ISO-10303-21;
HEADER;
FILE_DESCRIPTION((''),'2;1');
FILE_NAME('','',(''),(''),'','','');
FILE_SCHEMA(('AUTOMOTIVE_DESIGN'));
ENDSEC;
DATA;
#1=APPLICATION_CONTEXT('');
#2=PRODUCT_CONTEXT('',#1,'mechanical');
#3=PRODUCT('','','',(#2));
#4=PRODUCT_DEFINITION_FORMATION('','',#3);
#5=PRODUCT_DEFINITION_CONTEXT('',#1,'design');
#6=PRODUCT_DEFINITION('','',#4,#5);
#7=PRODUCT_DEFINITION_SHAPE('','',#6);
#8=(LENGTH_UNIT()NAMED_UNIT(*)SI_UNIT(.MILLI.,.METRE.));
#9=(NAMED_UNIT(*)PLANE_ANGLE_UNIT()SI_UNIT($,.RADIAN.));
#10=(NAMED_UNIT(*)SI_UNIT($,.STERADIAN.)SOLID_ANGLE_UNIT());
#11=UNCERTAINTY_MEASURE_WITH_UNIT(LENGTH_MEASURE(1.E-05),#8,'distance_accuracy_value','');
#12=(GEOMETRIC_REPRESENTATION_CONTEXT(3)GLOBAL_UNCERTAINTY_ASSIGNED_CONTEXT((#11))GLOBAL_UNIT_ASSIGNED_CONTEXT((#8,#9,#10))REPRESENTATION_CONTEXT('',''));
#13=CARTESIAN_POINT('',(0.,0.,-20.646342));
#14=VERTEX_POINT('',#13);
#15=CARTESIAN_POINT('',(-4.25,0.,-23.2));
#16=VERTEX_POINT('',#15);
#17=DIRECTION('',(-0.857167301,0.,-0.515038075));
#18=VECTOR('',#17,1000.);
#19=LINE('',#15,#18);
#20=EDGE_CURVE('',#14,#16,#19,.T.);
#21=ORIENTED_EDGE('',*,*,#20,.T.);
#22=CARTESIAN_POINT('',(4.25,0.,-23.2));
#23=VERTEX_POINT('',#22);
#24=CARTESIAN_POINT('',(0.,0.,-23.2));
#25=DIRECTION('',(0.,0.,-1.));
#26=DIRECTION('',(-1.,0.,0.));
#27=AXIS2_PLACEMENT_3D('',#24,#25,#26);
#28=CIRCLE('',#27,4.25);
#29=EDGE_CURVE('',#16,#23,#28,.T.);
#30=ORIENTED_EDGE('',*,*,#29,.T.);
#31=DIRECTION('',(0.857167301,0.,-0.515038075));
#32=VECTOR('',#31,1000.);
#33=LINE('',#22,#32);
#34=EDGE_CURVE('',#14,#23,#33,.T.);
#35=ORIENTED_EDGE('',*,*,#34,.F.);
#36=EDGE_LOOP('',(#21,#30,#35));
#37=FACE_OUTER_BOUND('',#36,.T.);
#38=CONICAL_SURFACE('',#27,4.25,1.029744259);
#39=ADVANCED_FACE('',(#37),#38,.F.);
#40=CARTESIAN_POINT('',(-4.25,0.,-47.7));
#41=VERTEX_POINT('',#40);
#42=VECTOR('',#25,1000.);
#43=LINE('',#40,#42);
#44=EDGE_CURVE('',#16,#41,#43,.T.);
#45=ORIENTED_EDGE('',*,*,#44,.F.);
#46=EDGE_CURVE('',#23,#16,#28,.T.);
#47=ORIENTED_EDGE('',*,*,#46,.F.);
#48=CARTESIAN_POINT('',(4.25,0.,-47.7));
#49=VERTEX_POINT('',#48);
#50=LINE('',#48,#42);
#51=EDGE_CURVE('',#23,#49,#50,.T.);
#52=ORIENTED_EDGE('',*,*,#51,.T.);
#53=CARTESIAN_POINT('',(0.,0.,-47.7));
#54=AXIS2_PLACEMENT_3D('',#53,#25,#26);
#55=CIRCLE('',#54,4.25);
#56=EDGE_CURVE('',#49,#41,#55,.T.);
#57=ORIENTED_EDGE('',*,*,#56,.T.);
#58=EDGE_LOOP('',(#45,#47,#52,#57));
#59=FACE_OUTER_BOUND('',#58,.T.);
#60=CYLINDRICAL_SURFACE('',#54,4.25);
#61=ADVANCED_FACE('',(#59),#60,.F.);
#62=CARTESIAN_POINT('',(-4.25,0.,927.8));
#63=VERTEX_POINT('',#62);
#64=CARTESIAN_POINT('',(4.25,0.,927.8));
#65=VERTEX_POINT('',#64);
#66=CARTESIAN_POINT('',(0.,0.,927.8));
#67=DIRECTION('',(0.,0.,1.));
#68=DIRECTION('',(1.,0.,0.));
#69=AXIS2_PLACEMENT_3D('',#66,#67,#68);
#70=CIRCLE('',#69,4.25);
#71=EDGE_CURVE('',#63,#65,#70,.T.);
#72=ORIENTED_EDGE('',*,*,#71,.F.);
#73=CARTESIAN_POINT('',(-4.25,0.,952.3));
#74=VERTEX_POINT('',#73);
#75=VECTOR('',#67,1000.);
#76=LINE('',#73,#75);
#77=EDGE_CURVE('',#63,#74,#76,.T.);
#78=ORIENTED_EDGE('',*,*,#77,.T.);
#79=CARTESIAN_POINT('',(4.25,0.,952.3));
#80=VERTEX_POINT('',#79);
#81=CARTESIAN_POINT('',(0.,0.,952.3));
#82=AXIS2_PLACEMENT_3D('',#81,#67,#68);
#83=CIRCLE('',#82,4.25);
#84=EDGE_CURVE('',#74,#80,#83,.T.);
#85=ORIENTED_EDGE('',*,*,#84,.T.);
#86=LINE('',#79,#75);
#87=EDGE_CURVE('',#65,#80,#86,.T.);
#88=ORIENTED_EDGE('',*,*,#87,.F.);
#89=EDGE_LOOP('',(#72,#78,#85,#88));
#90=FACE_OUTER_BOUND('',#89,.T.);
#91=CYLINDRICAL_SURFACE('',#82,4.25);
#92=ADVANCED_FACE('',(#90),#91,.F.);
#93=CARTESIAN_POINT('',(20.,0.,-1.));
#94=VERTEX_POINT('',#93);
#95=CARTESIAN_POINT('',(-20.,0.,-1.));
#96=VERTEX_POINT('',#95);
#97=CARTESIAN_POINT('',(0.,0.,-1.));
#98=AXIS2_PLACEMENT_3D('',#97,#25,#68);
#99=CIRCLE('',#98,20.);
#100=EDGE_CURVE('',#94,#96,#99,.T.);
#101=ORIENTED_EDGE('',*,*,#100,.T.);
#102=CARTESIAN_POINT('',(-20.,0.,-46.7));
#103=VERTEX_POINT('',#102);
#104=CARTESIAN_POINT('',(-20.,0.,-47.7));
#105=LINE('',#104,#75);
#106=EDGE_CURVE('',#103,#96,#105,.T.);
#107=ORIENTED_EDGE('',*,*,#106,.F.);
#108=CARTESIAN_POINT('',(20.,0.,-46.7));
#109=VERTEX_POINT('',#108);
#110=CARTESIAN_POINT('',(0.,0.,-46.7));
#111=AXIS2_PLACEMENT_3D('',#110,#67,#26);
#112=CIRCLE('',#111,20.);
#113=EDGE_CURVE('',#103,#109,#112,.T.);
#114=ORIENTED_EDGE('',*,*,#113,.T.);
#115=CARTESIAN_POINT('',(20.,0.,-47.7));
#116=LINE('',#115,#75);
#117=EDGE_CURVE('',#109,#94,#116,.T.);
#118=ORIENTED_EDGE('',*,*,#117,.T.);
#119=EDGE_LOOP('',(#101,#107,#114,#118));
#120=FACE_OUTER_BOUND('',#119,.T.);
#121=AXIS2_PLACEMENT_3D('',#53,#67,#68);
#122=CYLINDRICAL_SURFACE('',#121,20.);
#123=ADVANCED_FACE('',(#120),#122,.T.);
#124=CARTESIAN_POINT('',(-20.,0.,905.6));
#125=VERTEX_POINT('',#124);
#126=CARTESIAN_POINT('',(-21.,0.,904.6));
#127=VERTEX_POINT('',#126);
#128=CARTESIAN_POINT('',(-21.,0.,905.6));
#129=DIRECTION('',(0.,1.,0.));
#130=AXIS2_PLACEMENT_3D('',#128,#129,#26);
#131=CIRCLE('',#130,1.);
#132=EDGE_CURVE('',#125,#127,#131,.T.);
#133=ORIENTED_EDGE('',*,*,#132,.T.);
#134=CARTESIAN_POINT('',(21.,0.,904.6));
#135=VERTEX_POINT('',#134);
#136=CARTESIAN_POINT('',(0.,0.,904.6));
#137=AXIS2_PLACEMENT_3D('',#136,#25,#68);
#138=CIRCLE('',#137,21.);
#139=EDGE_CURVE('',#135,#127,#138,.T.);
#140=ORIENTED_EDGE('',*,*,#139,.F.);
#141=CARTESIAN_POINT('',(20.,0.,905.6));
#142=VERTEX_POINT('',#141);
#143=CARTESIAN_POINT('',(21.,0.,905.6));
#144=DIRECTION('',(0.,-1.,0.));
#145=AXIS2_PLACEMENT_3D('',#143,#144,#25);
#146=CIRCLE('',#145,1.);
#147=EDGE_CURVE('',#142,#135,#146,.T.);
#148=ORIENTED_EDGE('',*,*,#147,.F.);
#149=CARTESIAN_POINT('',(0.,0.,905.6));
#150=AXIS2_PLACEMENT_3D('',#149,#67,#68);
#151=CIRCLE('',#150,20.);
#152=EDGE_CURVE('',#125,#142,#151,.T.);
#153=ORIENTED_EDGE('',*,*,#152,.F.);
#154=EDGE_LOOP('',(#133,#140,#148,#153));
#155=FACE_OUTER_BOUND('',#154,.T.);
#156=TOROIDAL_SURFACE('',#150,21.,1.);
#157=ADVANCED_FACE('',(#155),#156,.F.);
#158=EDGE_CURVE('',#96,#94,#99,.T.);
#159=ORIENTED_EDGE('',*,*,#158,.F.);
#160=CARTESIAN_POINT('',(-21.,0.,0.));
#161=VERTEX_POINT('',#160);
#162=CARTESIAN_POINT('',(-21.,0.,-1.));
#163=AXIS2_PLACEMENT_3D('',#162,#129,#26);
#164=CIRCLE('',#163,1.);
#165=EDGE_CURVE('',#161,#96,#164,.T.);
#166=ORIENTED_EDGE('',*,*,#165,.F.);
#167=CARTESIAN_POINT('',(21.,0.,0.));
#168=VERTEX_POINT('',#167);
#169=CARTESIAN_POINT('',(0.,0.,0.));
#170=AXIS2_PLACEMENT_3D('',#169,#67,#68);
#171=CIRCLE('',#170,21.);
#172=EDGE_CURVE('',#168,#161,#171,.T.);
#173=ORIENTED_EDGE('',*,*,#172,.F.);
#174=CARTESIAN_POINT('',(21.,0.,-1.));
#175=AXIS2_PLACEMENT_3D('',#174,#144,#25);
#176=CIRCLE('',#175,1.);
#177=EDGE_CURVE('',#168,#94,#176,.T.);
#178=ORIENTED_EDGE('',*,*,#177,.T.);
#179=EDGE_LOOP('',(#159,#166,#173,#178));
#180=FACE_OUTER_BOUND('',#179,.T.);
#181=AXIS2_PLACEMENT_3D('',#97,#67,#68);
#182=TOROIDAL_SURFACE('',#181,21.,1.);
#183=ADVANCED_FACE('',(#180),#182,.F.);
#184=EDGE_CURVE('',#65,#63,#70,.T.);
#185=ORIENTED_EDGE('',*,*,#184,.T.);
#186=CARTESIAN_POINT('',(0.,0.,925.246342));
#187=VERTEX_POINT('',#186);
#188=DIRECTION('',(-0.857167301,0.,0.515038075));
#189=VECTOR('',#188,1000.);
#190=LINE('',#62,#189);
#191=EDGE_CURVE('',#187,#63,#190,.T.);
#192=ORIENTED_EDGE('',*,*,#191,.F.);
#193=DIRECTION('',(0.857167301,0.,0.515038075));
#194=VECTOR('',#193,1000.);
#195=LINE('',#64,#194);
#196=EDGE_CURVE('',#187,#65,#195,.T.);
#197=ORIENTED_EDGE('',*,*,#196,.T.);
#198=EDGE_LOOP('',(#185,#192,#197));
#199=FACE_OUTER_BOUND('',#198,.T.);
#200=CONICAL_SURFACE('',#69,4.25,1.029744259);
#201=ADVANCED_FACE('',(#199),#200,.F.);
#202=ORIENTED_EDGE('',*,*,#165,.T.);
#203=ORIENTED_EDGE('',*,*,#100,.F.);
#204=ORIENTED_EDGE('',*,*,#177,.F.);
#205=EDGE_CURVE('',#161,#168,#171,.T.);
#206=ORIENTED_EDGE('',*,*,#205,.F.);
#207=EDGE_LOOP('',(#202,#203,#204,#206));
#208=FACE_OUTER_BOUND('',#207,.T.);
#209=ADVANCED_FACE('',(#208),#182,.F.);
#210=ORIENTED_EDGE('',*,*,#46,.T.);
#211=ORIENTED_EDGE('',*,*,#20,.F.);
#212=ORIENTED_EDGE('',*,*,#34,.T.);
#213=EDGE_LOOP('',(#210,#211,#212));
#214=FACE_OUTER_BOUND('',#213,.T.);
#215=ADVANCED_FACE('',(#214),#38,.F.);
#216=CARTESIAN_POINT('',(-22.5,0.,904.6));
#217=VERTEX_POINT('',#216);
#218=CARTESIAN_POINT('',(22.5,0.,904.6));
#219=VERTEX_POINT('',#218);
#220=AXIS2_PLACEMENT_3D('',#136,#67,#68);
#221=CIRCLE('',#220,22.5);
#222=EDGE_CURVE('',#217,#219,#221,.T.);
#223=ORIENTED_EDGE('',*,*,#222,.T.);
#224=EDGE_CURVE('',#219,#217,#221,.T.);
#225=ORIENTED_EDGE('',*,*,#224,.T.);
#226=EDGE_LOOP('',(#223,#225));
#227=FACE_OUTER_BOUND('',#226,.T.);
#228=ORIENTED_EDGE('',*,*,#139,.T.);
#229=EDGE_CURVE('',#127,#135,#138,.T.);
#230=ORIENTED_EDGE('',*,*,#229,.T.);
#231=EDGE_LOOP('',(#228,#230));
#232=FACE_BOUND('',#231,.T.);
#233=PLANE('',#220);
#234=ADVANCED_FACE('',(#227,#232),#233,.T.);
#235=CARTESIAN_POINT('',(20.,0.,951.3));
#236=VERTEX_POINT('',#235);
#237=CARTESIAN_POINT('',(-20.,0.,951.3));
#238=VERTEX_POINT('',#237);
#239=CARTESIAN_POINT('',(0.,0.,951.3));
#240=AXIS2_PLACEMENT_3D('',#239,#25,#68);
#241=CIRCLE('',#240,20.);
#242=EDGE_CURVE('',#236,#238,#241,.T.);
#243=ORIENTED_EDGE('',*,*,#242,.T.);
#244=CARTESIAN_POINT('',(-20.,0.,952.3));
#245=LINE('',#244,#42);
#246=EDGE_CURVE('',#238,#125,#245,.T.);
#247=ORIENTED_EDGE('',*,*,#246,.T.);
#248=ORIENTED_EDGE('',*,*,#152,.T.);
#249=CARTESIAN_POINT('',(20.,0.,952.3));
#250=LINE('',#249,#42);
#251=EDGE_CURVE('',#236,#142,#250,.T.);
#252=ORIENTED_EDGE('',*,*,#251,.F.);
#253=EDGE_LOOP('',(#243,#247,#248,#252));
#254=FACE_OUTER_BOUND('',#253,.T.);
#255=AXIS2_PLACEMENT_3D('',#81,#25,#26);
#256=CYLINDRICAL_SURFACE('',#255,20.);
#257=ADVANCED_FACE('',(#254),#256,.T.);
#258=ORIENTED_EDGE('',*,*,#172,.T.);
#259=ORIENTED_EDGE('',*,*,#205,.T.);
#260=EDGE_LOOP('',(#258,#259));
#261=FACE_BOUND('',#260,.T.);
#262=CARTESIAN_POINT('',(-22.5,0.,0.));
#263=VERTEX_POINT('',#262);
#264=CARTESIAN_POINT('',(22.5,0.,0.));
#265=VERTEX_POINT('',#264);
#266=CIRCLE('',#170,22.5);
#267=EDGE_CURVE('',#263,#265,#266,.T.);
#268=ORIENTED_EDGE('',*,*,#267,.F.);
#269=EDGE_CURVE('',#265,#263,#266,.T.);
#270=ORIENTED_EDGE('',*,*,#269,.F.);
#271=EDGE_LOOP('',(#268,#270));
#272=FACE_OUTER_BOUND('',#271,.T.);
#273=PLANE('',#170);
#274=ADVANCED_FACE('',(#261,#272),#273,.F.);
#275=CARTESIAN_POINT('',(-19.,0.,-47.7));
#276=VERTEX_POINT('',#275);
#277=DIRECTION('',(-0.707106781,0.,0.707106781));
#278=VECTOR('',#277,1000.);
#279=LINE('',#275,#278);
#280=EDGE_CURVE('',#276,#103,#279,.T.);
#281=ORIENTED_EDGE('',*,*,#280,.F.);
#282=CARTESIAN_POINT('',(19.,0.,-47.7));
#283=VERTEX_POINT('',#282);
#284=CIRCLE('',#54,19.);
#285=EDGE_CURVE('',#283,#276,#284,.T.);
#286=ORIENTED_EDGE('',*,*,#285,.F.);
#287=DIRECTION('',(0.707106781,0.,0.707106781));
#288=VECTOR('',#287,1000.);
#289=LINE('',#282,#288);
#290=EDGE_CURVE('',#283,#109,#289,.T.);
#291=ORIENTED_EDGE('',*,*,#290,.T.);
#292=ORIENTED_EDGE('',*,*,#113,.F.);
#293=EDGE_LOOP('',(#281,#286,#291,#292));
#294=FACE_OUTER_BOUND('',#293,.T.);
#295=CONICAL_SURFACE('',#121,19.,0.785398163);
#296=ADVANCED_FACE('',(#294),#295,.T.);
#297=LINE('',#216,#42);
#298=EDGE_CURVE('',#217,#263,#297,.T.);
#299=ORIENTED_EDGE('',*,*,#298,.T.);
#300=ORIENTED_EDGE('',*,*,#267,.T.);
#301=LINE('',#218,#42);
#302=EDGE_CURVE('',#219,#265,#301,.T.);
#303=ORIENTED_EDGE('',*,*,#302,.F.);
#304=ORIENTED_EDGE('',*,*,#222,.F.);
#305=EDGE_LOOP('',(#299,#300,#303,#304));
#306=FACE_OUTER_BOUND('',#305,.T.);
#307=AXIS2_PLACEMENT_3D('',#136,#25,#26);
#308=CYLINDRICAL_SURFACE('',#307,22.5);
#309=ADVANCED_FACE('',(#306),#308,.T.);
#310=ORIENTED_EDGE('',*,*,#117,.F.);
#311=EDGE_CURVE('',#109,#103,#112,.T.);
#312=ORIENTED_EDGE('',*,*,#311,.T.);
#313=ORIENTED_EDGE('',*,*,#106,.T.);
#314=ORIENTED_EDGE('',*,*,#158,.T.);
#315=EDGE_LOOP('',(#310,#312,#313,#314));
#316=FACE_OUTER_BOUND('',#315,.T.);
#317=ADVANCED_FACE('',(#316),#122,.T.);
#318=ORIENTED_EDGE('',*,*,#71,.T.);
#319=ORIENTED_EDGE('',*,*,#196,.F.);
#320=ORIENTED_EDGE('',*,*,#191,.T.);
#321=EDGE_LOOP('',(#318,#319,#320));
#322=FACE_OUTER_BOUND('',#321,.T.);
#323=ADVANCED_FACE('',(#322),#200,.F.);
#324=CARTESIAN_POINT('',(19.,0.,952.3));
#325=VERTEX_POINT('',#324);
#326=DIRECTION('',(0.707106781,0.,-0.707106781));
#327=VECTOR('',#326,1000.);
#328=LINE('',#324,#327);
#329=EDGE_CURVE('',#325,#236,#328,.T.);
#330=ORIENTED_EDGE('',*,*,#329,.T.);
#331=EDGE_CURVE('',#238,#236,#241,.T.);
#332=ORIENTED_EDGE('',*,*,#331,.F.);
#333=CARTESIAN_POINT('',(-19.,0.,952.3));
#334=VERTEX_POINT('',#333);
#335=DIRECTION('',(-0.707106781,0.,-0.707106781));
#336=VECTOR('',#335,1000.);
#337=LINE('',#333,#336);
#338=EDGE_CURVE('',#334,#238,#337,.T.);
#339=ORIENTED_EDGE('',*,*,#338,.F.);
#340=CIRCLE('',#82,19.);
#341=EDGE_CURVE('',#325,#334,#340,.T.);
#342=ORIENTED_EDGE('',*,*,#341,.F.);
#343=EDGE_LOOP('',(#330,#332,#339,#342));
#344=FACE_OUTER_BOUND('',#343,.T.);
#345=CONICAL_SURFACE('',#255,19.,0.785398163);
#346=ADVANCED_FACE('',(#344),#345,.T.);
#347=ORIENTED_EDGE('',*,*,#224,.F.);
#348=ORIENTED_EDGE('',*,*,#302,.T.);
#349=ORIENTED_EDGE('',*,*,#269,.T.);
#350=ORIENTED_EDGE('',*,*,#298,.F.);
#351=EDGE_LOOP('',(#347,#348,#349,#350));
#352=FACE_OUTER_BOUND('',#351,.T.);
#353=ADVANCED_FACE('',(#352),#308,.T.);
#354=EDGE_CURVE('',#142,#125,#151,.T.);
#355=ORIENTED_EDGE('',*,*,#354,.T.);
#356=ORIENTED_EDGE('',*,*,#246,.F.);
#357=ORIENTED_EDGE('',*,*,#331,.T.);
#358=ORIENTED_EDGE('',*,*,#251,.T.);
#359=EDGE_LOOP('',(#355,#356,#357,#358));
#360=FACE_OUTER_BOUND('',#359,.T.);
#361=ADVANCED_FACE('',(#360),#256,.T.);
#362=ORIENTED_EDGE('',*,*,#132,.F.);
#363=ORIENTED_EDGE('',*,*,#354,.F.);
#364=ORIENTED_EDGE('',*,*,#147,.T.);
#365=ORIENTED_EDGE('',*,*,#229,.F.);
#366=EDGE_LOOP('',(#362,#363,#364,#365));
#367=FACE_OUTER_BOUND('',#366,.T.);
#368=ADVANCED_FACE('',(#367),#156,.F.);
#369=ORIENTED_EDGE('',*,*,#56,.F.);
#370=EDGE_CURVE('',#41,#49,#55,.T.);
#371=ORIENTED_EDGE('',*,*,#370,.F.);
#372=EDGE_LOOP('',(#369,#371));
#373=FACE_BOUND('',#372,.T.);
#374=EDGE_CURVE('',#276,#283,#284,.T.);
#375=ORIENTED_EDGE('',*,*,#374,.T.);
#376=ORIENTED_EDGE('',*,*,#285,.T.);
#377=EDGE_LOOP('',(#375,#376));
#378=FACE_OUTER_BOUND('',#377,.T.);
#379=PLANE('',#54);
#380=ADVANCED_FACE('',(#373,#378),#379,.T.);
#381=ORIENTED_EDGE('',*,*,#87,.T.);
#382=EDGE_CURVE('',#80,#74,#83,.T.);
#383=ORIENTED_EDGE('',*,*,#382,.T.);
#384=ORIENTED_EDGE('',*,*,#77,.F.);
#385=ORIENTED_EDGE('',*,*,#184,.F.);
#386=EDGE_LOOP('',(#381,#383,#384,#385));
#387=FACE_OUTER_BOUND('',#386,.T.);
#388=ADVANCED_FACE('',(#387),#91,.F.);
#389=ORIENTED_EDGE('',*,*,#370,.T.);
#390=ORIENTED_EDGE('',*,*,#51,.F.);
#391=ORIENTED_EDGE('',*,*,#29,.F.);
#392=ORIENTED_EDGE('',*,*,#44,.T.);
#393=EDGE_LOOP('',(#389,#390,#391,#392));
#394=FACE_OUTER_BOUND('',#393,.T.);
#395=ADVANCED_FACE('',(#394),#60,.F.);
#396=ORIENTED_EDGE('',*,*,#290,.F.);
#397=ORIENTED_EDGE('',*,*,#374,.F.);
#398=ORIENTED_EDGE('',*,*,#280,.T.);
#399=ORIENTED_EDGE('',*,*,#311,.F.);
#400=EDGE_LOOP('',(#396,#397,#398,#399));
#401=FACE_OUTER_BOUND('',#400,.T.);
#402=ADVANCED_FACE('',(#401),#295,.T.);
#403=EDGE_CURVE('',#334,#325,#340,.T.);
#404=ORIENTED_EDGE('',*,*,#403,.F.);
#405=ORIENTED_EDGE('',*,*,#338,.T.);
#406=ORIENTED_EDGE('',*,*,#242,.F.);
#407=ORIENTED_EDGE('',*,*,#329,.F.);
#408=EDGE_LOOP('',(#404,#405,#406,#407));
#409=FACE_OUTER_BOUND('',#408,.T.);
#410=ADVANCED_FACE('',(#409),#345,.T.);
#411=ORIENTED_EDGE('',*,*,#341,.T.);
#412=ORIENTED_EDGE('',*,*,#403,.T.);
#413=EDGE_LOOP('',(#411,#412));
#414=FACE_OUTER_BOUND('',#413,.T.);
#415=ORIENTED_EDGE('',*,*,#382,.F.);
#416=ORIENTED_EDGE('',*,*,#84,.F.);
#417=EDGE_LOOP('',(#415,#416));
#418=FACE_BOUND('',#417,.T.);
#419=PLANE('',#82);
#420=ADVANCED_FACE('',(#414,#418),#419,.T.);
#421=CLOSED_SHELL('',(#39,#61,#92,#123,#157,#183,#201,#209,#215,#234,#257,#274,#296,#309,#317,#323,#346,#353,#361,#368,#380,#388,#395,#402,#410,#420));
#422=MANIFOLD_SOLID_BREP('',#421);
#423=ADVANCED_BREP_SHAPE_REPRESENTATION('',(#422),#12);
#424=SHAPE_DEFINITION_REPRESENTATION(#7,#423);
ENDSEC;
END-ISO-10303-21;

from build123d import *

# Parameters (mm, degrees)
SKETCH_1_R              = 22.5
EXTRUDE_1_DEPTH         = 904.6
SKETCH_2_R              = 20
EXTRUDE_2_DEPTH         = 47.7
EXTRUDE_START           = 47.7
SKETCH_3_R              = 20
EXTRUDE_3_DEPTH         = 47.7
FILLET_1_R              = 1
CHAMFER_1_SIZE          = 1
HOLE_WIZARD_M10_1_D     = 8.5
HOLE_WIZARD_M10_1_DEPTH = 24.5
HOLE_WIZARD_M10_1_TIP   = 2.553657631
HOLE_WIZARD_M10_2_D     = 8.5
HOLE_WIZARD_M10_2_DEPTH = 24.5
HOLE_WIZARD_M10_2_TIP   = 2.553657631


with BuildPart() as part:
    # 草图1 → 凸台-拉伸1 (new body)
    with BuildSketch(Plane.XY):
        with Locations(Location((0, 0, 0), (0, 0, 180))):
            Circle(SKETCH_1_R)
    extrude(amount=EXTRUDE_1_DEPTH)

    # 草图2 → 凸台-拉伸2 (add)
    with BuildSketch(Plane.XY.offset(904.6)):
        Circle(SKETCH_2_R)
    extrude(amount=EXTRUDE_2_DEPTH)

    # 草图3 → 凸台-拉伸3 (add)
    with BuildSketch(Plane(origin=(0, 0, 0), x_dir=(-1, 0, 0), z_dir=(0, 0, -1)).offset(EXTRUDE_START)):
        with Locations(Location((0, 0, 0), (0, 0, 180))):
            Circle(SKETCH_3_R)
    extrude(amount=-EXTRUDE_3_DEPTH)

    # 圆角1
    fillet_1_edges = [part.edges().sort_by_distance(p)[0] for p in [
        (-20, 0, 904.6),
        (-20, 0, 0),
    ]]
    fillet(fillet_1_edges, radius=FILLET_1_R)

    # 倒角1
    chamfer_1_edges = [part.edges().sort_by_distance(p)[0] for p in [
        (-20, 0, -47.7),
        (-20, 0, 952.3),
    ]]
    chamfer(chamfer_1_edges, length=CHAMFER_1_SIZE)

    # M10 螺纹孔1
    with Locations(Plane.XY.offset(952.3)):
        with Locations((0, 0)):
            Hole(HOLE_WIZARD_M10_1_D / 2, depth=HOLE_WIZARD_M10_1_DEPTH)
            with Locations((0, 0, -(HOLE_WIZARD_M10_1_DEPTH + HOLE_WIZARD_M10_1_TIP / 2))):  # 118° drill point
                Cone(0, HOLE_WIZARD_M10_1_D / 2, HOLE_WIZARD_M10_1_TIP, mode=Mode.SUBTRACT)

    # M10 螺纹孔2
    with Locations(Plane(origin=(0, 0, -47.7), x_dir=(-1, 0, 0), z_dir=(0, 0, -1))):
        with Locations((0, 0)):
            Hole(HOLE_WIZARD_M10_2_D / 2, depth=HOLE_WIZARD_M10_2_DEPTH)
            with Locations((0, 0, -(HOLE_WIZARD_M10_2_DEPTH + HOLE_WIZARD_M10_2_TIP / 2))):  # 118° drill point
                Cone(0, HOLE_WIZARD_M10_2_D / 2, HOLE_WIZARD_M10_2_TIP, mode=Mode.SUBTRACT)


solid = part.part
